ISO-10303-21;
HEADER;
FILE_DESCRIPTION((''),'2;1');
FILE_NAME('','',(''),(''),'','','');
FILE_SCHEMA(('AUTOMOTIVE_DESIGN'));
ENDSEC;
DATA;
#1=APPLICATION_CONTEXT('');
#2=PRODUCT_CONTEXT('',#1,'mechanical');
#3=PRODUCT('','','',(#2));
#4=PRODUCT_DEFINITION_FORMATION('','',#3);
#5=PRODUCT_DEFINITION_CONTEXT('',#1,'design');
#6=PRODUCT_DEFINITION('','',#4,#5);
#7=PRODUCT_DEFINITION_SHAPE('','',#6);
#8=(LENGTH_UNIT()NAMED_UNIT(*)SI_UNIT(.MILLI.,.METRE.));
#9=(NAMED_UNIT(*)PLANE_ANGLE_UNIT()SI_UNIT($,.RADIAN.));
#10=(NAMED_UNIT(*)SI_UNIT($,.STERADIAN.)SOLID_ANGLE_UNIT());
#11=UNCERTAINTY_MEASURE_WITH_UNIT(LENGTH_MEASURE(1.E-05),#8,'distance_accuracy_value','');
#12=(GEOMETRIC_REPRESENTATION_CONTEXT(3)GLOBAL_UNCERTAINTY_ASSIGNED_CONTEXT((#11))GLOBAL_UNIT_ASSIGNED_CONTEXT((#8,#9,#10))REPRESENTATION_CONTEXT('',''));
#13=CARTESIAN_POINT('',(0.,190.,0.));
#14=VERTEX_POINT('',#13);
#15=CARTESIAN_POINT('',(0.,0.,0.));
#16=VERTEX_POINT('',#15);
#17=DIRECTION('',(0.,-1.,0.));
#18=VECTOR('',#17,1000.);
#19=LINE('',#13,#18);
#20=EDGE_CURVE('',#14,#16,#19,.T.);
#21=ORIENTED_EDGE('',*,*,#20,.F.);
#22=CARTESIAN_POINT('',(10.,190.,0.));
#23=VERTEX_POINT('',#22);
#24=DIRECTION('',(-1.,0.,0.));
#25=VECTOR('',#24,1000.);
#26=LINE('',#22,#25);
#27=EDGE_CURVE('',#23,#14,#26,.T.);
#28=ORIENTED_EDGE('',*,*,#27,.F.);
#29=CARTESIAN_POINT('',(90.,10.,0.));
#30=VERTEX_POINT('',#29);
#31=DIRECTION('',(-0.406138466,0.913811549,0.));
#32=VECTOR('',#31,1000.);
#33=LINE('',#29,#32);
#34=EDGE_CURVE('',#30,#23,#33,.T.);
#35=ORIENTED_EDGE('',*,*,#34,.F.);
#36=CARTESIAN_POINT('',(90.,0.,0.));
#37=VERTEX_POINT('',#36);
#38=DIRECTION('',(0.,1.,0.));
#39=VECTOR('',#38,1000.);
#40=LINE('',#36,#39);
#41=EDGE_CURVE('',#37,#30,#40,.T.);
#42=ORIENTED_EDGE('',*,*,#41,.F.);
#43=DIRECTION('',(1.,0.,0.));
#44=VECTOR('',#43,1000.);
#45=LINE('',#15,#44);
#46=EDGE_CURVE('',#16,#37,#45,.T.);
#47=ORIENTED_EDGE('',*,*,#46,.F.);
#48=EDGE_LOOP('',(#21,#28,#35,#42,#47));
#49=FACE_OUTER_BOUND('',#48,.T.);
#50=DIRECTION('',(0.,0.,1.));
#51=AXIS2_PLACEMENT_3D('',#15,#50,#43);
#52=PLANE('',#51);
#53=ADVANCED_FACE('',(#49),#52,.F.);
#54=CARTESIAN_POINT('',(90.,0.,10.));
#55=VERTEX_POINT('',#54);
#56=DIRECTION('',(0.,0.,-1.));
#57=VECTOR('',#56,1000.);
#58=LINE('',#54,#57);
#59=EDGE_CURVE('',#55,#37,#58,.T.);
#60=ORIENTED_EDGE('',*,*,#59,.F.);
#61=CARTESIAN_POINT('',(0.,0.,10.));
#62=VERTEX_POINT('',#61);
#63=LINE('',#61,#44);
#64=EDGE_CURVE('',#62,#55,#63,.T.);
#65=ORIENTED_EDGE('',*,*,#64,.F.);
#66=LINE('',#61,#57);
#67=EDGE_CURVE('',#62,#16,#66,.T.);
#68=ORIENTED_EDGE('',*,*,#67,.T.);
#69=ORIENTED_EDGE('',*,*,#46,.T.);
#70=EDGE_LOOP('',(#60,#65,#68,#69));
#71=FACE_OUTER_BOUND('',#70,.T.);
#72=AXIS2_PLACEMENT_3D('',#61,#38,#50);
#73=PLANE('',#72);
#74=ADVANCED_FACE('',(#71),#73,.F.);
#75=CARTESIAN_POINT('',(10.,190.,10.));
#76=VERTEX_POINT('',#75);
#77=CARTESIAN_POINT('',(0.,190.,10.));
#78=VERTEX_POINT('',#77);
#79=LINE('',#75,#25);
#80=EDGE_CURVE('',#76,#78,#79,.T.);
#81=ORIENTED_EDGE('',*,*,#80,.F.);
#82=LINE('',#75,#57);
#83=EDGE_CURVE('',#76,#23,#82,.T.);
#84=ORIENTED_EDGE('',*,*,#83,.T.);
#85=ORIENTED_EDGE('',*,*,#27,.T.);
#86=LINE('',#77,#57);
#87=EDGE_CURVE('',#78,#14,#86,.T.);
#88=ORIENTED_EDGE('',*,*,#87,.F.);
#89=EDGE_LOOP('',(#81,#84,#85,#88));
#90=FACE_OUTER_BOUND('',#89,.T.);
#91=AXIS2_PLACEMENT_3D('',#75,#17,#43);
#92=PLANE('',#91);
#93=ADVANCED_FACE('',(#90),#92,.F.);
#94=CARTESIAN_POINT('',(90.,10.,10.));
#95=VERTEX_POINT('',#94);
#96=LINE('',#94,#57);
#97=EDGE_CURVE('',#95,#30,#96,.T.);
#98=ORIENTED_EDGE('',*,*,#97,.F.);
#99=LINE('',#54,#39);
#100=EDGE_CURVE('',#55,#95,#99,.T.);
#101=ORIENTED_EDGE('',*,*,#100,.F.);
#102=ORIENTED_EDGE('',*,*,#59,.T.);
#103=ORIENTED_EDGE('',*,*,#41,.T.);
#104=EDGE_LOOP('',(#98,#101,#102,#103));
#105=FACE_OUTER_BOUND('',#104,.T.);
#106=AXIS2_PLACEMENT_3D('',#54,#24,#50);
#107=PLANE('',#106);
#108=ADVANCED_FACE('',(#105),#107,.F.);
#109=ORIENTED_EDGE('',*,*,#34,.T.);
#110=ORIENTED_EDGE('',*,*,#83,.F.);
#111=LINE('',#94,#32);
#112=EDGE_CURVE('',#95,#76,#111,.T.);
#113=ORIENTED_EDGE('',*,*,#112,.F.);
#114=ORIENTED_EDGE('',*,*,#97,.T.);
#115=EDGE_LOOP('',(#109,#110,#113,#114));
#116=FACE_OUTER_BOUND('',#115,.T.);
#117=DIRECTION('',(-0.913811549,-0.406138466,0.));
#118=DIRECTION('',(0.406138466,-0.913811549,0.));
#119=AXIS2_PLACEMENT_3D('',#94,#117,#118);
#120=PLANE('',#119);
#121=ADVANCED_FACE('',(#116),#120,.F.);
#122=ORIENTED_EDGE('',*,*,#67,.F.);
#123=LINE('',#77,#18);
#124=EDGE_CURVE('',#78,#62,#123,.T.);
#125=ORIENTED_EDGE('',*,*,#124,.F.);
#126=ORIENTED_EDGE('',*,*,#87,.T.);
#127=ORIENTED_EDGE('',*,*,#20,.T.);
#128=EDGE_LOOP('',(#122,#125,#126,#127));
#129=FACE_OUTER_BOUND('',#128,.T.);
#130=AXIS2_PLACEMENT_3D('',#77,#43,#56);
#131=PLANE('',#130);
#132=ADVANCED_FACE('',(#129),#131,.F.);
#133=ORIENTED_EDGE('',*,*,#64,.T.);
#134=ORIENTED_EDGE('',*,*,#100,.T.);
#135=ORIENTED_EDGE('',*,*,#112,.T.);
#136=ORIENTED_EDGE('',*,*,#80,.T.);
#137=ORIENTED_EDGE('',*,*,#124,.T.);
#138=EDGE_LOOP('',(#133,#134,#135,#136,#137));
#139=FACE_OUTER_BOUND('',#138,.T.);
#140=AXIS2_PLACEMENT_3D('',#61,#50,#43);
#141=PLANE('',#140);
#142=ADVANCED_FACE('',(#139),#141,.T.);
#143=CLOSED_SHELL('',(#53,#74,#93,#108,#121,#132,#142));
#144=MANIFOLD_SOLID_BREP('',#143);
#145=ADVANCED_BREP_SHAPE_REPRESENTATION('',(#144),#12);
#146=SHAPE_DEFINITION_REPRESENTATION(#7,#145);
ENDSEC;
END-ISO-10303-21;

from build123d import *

# Parameters (mm, degrees)
BOSS_EXTRUDE1_DEPTH = 10


with BuildPart() as part:
    # Sketch1 → Boss-Extrude1 (new body)
    with BuildSketch(Plane.XY):
        Polygon((0, 0), (90, 0), (90, 10), (10, 190), (0, 190), align=None)
    extrude(amount=BOSS_EXTRUDE1_DEPTH)


solid = part.part
